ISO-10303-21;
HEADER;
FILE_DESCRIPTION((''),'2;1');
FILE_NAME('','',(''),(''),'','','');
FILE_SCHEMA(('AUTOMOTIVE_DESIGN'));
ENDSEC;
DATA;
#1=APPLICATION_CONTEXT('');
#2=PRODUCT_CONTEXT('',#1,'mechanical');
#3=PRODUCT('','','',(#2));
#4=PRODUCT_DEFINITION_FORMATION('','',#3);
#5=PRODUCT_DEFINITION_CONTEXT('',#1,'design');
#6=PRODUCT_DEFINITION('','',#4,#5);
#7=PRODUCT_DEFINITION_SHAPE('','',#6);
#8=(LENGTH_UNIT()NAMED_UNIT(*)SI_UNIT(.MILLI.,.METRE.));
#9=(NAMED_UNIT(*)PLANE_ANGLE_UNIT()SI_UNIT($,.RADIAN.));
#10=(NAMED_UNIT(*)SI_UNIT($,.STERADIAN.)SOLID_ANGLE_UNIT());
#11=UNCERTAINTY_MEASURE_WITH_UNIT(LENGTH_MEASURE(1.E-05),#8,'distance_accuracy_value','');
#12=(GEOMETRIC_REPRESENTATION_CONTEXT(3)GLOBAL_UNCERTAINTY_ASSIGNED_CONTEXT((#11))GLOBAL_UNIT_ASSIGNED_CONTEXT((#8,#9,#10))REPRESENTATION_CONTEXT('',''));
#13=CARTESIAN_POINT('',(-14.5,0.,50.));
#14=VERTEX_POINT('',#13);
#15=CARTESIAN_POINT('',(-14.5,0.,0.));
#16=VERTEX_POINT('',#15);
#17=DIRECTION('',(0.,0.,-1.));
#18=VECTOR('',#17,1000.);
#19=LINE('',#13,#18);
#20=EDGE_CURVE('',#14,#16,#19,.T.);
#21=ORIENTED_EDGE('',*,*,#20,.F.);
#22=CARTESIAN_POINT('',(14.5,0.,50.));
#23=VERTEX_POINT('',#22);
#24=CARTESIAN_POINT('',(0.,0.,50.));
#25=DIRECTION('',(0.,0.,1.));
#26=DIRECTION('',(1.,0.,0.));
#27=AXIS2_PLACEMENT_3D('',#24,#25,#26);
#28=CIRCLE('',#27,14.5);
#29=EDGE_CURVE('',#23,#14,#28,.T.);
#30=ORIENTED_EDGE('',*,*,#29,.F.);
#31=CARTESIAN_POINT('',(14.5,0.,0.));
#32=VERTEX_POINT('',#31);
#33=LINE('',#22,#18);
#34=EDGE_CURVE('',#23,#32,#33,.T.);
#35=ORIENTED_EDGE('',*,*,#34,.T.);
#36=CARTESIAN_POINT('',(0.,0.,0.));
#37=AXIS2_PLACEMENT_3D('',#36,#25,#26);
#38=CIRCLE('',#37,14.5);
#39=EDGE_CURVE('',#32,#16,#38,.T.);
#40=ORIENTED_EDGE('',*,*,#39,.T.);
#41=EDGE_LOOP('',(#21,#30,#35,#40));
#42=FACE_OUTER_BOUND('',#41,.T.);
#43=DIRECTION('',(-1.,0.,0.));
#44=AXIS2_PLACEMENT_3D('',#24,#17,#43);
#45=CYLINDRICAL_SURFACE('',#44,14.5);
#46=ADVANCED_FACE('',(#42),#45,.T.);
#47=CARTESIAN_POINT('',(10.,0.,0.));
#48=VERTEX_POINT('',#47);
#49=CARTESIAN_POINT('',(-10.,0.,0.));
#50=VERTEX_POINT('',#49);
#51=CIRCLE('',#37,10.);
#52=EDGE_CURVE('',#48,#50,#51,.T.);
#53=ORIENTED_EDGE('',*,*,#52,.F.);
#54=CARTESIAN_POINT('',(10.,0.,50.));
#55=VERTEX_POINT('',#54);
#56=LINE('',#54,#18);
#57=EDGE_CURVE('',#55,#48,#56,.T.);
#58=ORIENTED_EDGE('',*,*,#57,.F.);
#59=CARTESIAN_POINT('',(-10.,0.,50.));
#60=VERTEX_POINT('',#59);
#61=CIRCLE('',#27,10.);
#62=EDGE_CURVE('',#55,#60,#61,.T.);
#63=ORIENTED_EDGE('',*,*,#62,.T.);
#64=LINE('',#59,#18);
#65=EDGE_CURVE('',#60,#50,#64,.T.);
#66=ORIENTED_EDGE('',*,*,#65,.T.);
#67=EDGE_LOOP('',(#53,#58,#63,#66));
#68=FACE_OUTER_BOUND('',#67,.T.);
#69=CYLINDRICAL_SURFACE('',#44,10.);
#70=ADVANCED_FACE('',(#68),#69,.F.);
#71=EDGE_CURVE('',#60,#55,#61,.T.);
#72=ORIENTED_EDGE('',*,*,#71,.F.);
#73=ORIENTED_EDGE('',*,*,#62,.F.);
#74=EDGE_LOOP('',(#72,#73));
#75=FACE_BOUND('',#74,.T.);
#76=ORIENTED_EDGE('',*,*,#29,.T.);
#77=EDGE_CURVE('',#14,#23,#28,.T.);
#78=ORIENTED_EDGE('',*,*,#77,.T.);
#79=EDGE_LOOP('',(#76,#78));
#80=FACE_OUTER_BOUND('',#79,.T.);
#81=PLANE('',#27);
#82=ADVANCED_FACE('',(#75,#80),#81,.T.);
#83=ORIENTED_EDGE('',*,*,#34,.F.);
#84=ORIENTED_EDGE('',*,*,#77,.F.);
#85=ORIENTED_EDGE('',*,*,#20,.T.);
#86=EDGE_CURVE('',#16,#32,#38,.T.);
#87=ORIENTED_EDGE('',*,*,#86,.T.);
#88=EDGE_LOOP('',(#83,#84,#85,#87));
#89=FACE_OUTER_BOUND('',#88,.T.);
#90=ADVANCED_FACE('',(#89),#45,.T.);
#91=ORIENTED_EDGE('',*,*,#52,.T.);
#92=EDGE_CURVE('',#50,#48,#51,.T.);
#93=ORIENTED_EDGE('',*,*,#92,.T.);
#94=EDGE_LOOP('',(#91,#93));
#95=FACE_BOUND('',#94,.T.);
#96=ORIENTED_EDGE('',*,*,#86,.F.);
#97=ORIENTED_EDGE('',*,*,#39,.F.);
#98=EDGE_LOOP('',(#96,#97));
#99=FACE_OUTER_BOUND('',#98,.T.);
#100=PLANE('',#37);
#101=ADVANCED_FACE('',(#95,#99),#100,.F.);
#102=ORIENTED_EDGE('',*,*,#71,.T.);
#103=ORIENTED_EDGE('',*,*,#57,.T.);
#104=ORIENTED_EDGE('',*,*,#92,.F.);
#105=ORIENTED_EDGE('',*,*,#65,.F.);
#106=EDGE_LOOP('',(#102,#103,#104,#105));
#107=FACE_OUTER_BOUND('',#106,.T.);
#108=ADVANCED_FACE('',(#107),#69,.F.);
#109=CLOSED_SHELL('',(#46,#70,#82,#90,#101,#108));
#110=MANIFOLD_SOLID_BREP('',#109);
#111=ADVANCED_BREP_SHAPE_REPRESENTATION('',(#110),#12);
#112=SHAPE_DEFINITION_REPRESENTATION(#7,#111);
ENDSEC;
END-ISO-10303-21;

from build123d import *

# Parameters (mm, degrees)
SKETCH_1_R      = 14.5
SKETCH_1_R_2    = 10
EXTRUDE_1_DEPTH = 50


with BuildPart() as part:
    # 草图1 → 凸台-拉伸1 (new body)
    with BuildSketch(Plane.XY):
        Circle(SKETCH_1_R)
        Circle(SKETCH_1_R_2, mode=Mode.SUBTRACT)
    extrude(amount=EXTRUDE_1_DEPTH)


solid = part.part
